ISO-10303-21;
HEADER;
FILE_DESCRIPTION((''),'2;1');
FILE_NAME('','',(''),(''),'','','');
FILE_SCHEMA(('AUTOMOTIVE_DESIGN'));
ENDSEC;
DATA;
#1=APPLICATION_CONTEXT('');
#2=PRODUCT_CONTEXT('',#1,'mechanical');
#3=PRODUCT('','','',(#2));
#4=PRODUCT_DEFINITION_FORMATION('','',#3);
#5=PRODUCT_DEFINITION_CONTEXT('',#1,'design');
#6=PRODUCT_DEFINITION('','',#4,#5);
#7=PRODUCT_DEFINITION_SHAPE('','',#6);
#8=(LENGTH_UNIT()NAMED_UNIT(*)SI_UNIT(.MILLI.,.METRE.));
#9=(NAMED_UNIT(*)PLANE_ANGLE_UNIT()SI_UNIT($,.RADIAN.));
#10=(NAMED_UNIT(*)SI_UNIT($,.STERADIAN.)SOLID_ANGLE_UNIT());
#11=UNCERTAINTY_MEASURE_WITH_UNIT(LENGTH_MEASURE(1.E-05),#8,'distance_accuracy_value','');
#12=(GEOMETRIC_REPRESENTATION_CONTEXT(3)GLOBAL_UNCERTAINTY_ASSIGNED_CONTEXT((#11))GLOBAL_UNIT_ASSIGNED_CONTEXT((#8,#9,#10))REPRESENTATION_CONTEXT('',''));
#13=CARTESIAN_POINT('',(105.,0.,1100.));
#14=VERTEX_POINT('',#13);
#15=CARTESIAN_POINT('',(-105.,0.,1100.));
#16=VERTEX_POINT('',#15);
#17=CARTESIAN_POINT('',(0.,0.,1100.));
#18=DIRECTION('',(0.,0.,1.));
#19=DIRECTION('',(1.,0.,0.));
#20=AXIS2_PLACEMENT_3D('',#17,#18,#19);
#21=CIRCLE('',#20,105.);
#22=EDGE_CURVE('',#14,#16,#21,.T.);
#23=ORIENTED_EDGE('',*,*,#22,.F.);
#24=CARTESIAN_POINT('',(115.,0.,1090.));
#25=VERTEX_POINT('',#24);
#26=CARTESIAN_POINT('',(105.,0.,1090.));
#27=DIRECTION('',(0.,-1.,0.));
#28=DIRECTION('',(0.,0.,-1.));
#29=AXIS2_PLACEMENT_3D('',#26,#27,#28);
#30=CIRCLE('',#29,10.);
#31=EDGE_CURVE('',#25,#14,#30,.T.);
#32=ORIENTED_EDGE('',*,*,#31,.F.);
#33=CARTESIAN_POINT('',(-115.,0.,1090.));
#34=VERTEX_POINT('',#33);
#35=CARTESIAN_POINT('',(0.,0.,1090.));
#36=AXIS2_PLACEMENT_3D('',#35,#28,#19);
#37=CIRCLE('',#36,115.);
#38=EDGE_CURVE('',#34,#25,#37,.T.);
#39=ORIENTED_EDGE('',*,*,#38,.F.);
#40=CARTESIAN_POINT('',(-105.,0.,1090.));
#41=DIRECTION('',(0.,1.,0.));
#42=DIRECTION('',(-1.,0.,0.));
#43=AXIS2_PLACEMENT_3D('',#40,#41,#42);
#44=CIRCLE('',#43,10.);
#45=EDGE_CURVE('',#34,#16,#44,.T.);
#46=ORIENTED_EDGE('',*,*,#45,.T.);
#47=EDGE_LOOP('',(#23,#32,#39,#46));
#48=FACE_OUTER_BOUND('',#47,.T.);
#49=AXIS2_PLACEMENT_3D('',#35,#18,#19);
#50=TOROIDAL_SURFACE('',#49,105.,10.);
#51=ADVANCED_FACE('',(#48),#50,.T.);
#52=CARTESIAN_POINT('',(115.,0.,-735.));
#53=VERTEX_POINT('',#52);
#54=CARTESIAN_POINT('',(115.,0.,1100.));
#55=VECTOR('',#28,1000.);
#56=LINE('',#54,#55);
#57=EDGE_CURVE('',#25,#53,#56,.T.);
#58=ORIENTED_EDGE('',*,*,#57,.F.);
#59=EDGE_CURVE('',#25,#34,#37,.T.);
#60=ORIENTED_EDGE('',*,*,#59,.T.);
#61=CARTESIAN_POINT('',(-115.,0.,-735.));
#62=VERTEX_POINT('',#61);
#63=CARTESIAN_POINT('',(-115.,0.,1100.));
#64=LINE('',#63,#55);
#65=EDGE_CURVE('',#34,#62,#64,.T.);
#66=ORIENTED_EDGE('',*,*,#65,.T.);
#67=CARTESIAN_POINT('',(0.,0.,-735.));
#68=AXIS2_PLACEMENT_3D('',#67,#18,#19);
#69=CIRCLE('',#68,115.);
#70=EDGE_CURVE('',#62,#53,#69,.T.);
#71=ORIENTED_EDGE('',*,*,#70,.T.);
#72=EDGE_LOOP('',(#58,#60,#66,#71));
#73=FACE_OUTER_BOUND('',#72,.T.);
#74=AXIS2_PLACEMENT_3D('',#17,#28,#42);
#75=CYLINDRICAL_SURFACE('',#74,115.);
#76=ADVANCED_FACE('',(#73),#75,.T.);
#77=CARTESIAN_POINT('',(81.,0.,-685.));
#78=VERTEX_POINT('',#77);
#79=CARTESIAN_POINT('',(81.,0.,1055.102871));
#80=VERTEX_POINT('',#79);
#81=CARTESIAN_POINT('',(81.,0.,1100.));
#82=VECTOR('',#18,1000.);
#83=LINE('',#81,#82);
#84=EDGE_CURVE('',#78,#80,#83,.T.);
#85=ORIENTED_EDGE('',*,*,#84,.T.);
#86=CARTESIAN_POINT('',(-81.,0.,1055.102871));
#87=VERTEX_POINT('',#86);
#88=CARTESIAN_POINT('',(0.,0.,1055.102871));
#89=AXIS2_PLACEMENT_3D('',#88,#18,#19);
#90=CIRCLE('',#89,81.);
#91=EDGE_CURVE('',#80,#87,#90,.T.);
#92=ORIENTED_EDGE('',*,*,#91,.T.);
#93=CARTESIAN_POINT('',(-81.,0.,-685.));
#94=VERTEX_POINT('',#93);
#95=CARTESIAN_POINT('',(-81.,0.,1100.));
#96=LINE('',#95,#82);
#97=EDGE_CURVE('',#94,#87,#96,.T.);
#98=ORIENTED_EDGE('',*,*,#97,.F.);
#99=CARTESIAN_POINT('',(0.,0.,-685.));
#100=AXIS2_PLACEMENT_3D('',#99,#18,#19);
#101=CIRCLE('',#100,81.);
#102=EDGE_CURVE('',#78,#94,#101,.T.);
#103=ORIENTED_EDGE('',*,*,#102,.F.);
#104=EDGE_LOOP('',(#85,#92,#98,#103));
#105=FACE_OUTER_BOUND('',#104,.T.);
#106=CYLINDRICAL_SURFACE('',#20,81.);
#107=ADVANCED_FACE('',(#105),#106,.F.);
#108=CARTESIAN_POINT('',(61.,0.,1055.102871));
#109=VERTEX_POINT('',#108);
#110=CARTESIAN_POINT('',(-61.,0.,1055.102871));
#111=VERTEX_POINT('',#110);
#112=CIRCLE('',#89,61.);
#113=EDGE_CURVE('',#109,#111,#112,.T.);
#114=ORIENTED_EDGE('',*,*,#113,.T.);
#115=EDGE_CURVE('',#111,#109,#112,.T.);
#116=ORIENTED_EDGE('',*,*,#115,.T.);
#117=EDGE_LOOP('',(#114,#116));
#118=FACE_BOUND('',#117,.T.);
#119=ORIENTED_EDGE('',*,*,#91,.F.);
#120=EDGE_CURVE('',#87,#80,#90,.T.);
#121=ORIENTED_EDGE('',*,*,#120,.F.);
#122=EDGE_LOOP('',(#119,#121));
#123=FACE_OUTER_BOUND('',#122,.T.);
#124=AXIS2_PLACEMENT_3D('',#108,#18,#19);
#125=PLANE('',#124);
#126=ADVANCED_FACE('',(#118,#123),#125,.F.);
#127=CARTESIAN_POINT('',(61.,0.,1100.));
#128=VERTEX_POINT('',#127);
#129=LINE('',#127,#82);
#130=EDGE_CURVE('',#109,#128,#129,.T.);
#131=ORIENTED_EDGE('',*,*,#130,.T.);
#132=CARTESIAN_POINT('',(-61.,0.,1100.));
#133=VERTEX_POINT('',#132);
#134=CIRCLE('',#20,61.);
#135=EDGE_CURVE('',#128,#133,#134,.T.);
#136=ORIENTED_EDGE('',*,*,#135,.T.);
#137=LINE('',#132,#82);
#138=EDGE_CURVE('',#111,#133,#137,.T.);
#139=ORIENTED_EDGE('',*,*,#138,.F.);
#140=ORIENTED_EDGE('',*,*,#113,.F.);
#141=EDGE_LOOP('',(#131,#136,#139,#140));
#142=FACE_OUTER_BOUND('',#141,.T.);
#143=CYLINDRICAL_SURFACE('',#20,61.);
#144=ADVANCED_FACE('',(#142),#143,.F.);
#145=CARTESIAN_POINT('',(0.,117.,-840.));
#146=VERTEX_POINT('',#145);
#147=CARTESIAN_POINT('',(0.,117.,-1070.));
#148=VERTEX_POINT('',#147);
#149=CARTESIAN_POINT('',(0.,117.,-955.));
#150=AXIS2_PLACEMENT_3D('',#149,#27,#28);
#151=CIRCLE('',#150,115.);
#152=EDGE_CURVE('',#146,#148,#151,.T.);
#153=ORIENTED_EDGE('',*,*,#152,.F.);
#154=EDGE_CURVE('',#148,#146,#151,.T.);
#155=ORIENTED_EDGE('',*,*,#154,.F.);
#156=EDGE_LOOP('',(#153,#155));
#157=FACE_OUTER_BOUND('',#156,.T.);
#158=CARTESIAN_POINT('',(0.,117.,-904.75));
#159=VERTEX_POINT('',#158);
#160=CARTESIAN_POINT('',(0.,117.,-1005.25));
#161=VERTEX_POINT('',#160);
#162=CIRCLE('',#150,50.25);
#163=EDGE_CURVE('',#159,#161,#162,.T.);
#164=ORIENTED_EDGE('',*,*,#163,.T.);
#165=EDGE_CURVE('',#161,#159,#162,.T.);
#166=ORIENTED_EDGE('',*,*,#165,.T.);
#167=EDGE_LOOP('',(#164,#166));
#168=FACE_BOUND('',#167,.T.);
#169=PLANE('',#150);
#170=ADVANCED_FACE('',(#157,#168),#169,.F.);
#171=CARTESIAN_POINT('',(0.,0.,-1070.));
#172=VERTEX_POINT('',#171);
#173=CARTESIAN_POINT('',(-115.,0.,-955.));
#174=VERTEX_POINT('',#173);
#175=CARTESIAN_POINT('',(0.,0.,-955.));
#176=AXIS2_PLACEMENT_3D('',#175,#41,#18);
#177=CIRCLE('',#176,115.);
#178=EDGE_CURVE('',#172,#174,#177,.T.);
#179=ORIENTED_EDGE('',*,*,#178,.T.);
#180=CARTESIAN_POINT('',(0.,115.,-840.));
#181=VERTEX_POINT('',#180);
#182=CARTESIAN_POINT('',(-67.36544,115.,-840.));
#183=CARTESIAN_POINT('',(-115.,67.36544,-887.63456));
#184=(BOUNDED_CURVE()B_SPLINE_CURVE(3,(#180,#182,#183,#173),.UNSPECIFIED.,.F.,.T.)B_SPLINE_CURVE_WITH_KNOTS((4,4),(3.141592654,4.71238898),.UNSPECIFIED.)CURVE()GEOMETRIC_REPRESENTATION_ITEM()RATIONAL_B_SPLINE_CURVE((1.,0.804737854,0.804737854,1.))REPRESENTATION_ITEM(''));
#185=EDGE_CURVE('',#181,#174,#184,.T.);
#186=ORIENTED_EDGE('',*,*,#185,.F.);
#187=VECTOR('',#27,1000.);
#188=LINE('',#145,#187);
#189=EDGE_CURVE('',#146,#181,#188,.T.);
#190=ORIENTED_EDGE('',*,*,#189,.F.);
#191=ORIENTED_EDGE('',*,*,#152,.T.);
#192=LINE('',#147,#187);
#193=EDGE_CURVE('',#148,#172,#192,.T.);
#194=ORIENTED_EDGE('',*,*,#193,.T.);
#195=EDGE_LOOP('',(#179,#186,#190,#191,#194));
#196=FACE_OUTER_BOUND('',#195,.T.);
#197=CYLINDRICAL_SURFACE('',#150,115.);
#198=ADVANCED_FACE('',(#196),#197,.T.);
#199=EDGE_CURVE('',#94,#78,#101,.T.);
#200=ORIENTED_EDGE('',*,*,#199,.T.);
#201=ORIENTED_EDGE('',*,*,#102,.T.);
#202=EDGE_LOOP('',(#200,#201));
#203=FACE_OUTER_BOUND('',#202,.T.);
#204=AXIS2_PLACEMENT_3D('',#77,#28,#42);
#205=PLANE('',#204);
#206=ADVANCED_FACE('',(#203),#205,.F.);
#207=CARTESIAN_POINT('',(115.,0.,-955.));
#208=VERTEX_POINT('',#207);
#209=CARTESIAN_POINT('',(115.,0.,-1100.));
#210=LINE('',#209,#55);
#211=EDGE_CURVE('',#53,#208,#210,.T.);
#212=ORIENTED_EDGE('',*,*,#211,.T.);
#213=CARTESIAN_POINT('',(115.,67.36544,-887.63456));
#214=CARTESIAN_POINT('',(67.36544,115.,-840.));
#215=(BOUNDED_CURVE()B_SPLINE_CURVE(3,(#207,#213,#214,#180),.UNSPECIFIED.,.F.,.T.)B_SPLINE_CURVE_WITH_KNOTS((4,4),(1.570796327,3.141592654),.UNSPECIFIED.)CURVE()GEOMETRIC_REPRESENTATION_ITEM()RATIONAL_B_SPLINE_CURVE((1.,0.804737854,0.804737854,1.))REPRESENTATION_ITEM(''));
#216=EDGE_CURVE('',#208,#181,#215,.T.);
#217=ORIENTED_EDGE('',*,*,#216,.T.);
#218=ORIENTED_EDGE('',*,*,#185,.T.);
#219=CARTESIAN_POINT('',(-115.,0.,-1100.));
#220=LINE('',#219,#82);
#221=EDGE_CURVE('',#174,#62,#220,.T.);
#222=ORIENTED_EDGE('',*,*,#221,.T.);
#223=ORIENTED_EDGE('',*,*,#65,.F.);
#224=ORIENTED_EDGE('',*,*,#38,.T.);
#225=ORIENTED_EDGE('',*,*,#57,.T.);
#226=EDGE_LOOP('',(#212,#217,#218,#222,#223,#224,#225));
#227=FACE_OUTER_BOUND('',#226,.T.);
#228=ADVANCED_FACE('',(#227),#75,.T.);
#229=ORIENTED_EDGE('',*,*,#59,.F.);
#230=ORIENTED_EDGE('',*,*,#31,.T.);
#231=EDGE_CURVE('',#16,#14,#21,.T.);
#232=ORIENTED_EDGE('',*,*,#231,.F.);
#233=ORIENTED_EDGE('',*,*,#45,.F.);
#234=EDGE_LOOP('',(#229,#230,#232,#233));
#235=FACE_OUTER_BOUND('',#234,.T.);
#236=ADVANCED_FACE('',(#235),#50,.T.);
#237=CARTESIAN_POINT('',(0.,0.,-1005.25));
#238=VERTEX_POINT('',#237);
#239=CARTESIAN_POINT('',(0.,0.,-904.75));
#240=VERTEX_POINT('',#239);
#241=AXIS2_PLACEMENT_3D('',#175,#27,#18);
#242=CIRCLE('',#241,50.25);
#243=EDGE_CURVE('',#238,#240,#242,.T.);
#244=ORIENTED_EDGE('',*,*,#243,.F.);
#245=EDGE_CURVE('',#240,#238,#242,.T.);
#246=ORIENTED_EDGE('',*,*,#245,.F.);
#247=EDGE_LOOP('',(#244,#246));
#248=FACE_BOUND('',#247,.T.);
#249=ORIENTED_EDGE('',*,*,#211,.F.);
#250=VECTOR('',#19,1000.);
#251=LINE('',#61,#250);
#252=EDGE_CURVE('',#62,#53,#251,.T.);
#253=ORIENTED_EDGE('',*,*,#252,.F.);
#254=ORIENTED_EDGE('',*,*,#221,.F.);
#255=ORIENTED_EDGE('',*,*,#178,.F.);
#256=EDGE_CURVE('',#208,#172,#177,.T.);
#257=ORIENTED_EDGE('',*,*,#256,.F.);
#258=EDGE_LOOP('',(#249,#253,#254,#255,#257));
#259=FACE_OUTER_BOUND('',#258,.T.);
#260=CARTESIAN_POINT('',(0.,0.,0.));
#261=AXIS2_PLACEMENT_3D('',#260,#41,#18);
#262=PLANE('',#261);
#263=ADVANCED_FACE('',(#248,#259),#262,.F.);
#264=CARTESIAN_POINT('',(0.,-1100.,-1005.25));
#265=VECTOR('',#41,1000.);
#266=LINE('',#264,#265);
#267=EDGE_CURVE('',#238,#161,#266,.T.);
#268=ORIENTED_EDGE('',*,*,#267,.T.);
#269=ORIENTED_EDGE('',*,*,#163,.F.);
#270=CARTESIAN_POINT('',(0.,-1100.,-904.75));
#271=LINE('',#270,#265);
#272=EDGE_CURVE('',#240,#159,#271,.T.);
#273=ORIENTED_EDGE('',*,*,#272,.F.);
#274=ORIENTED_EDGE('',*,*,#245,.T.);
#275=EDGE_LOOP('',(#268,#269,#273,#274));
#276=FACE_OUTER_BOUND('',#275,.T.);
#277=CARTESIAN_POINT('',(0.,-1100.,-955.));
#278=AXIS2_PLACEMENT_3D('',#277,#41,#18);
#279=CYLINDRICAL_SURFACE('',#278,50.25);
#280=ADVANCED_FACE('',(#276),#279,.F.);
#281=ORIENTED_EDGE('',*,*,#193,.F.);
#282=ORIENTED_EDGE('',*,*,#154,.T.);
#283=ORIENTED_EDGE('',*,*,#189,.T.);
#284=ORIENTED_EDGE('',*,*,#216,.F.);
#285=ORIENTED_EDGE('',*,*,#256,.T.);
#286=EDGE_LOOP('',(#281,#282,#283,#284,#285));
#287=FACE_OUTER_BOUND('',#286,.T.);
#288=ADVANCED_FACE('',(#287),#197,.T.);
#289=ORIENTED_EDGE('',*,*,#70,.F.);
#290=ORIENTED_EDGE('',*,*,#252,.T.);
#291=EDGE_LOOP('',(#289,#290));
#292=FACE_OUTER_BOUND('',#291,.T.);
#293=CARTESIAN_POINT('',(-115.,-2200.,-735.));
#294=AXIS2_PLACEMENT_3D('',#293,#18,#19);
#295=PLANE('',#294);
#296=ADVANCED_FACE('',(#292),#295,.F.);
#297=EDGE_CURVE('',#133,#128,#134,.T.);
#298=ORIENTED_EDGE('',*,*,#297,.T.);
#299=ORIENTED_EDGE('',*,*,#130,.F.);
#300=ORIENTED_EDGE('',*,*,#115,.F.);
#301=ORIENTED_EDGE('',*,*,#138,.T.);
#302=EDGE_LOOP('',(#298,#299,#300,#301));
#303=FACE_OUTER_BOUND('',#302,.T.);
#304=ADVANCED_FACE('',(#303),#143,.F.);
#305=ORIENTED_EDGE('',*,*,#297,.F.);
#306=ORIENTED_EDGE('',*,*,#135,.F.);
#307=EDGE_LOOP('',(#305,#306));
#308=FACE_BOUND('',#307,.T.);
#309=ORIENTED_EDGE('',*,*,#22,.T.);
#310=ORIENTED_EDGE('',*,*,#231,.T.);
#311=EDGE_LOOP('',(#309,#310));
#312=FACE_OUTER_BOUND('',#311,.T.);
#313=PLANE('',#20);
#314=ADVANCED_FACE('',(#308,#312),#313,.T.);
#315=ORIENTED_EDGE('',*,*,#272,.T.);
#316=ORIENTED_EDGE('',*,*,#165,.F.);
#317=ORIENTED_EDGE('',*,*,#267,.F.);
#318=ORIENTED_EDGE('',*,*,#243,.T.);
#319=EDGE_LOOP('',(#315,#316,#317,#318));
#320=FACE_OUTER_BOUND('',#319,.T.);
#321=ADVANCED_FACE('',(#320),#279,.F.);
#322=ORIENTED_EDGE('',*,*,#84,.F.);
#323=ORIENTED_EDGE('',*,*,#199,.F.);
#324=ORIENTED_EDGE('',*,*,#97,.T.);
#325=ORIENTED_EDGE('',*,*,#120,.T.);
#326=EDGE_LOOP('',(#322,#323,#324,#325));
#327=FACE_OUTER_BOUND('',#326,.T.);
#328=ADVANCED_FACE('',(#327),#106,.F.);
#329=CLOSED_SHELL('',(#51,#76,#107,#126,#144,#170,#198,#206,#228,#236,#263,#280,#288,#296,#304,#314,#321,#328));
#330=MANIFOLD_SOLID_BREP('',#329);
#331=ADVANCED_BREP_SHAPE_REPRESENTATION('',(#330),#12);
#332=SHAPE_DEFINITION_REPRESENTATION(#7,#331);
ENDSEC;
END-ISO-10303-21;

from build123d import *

# Parameters (mm, degrees)
BARREL_PROFILE_SKETCH_R  = 115
BARREL_BODY_230_DEPTH    = 1100
EYE_PIN_HOLE_SKETCH_R    = 50.25
EYE_PIN_HOLE_100_5_DEPTH = 1100
EYE_FLATS_SKETCH_W       = 230
EYE_FLATS_SKETCH_H       = 365
EYE_FLATS_CUT_DEPTH      = 2200
EYE_START                = -117
EYE_BOSS_SKETCH_R        = 115
EYE_BOSS_SKETCH_R_2      = 50.25
EYE_BOSS_EXTRUDE_DEPTH   = 117
EDGE_FILLET_R10_R        = 10


with BuildPart() as part:
    # Barrel Profile Sketch → Barrel Body Ø230 (new, symmetric)
    with BuildSketch(Plane.XY):
        Circle(BARREL_PROFILE_SKETCH_R)
    extrude(amount=BARREL_BODY_230_DEPTH, both=True)

    # Eye Pin Hole Sketch → Eye Pin Hole Ø100.5 (cut, symmetric)
    with BuildSketch(Plane(origin=(0, 0, 0), x_dir=(1, 0, 0), z_dir=(0, 1, 0))):
        with Locations(Location((0, 955, 0), (0, 0, 270))):
            Circle(EYE_PIN_HOLE_SKETCH_R)
    extrude(amount=EYE_PIN_HOLE_100_5_DEPTH, both=True, mode=Mode.SUBTRACT)

    # Eye Flats Sketch → Eye Flats Cut (cut)
    with BuildSketch(Plane(origin=(0, 0, 0), x_dir=(1, 0, 0), z_dir=(0, 1, 0))):
        with Locations((0, 917.5)):
            Rectangle(EYE_FLATS_SKETCH_W, EYE_FLATS_SKETCH_H)
    extrude(amount=-EYE_FLATS_CUT_DEPTH, mode=Mode.SUBTRACT)

    # Eye Transition Sketch → Eye Transition Revolve Cut (revolve, cut)
    with BuildSketch(Plane.XZ):
        with BuildLine():
            Line((-115, -955), (-196.346531204, -955))
            Line((-196.346531204, -955), (-196.346531204, -1191.859792513))
            Line((-196.346531204, -1191.859792513), (0, -1191.859792513))
            Line((0, -1191.859792513), (0, -1070))
            ThreePointArc((0, -1070), (-81.317279836, -1036.317279836), (-115, -955))
        make_face()
    revolve(axis=Axis((0, 0, -1191.859792513), (0, 0, 1)), mode=Mode.SUBTRACT)

    # End Bore Sketch → End Bore Revolve Cut (revolve, cut)
    with BuildSketch(Plane(origin=(0, 0, 0), x_dir=(1, 0, 0), z_dir=(0, 1, 0))):
        Polygon((0, -1100), (61, -1100), (61, -1055.102870795), (81, -1055.102870795), (81, 685), (0, 685), align=None)
    revolve(axis=Axis((0, 0, 1100), (0, 0, -1)), mode=Mode.SUBTRACT)

    # Eye Boss Sketch → Eye Boss Extrude (add)
    with BuildSketch(Plane.XZ.offset(EYE_START)):
        with Locations(Location((0, -955, 0), (0, 0, 270))):
            Circle(EYE_BOSS_SKETCH_R)
        with Locations(Location((0, -955, 0), (0, 0, 90))):
            Circle(EYE_BOSS_SKETCH_R_2, mode=Mode.SUBTRACT)
    extrude(amount=EYE_BOSS_EXTRUDE_DEPTH)

    # Edge Fillet R10
    edge_fillet_r10_edges = [part.edges().sort_by_distance(p)[0] for p in [
        (-115, 0, 1100),
    ]]
    fillet(edge_fillet_r10_edges, radius=EDGE_FILLET_R10_R)


solid = part.part
